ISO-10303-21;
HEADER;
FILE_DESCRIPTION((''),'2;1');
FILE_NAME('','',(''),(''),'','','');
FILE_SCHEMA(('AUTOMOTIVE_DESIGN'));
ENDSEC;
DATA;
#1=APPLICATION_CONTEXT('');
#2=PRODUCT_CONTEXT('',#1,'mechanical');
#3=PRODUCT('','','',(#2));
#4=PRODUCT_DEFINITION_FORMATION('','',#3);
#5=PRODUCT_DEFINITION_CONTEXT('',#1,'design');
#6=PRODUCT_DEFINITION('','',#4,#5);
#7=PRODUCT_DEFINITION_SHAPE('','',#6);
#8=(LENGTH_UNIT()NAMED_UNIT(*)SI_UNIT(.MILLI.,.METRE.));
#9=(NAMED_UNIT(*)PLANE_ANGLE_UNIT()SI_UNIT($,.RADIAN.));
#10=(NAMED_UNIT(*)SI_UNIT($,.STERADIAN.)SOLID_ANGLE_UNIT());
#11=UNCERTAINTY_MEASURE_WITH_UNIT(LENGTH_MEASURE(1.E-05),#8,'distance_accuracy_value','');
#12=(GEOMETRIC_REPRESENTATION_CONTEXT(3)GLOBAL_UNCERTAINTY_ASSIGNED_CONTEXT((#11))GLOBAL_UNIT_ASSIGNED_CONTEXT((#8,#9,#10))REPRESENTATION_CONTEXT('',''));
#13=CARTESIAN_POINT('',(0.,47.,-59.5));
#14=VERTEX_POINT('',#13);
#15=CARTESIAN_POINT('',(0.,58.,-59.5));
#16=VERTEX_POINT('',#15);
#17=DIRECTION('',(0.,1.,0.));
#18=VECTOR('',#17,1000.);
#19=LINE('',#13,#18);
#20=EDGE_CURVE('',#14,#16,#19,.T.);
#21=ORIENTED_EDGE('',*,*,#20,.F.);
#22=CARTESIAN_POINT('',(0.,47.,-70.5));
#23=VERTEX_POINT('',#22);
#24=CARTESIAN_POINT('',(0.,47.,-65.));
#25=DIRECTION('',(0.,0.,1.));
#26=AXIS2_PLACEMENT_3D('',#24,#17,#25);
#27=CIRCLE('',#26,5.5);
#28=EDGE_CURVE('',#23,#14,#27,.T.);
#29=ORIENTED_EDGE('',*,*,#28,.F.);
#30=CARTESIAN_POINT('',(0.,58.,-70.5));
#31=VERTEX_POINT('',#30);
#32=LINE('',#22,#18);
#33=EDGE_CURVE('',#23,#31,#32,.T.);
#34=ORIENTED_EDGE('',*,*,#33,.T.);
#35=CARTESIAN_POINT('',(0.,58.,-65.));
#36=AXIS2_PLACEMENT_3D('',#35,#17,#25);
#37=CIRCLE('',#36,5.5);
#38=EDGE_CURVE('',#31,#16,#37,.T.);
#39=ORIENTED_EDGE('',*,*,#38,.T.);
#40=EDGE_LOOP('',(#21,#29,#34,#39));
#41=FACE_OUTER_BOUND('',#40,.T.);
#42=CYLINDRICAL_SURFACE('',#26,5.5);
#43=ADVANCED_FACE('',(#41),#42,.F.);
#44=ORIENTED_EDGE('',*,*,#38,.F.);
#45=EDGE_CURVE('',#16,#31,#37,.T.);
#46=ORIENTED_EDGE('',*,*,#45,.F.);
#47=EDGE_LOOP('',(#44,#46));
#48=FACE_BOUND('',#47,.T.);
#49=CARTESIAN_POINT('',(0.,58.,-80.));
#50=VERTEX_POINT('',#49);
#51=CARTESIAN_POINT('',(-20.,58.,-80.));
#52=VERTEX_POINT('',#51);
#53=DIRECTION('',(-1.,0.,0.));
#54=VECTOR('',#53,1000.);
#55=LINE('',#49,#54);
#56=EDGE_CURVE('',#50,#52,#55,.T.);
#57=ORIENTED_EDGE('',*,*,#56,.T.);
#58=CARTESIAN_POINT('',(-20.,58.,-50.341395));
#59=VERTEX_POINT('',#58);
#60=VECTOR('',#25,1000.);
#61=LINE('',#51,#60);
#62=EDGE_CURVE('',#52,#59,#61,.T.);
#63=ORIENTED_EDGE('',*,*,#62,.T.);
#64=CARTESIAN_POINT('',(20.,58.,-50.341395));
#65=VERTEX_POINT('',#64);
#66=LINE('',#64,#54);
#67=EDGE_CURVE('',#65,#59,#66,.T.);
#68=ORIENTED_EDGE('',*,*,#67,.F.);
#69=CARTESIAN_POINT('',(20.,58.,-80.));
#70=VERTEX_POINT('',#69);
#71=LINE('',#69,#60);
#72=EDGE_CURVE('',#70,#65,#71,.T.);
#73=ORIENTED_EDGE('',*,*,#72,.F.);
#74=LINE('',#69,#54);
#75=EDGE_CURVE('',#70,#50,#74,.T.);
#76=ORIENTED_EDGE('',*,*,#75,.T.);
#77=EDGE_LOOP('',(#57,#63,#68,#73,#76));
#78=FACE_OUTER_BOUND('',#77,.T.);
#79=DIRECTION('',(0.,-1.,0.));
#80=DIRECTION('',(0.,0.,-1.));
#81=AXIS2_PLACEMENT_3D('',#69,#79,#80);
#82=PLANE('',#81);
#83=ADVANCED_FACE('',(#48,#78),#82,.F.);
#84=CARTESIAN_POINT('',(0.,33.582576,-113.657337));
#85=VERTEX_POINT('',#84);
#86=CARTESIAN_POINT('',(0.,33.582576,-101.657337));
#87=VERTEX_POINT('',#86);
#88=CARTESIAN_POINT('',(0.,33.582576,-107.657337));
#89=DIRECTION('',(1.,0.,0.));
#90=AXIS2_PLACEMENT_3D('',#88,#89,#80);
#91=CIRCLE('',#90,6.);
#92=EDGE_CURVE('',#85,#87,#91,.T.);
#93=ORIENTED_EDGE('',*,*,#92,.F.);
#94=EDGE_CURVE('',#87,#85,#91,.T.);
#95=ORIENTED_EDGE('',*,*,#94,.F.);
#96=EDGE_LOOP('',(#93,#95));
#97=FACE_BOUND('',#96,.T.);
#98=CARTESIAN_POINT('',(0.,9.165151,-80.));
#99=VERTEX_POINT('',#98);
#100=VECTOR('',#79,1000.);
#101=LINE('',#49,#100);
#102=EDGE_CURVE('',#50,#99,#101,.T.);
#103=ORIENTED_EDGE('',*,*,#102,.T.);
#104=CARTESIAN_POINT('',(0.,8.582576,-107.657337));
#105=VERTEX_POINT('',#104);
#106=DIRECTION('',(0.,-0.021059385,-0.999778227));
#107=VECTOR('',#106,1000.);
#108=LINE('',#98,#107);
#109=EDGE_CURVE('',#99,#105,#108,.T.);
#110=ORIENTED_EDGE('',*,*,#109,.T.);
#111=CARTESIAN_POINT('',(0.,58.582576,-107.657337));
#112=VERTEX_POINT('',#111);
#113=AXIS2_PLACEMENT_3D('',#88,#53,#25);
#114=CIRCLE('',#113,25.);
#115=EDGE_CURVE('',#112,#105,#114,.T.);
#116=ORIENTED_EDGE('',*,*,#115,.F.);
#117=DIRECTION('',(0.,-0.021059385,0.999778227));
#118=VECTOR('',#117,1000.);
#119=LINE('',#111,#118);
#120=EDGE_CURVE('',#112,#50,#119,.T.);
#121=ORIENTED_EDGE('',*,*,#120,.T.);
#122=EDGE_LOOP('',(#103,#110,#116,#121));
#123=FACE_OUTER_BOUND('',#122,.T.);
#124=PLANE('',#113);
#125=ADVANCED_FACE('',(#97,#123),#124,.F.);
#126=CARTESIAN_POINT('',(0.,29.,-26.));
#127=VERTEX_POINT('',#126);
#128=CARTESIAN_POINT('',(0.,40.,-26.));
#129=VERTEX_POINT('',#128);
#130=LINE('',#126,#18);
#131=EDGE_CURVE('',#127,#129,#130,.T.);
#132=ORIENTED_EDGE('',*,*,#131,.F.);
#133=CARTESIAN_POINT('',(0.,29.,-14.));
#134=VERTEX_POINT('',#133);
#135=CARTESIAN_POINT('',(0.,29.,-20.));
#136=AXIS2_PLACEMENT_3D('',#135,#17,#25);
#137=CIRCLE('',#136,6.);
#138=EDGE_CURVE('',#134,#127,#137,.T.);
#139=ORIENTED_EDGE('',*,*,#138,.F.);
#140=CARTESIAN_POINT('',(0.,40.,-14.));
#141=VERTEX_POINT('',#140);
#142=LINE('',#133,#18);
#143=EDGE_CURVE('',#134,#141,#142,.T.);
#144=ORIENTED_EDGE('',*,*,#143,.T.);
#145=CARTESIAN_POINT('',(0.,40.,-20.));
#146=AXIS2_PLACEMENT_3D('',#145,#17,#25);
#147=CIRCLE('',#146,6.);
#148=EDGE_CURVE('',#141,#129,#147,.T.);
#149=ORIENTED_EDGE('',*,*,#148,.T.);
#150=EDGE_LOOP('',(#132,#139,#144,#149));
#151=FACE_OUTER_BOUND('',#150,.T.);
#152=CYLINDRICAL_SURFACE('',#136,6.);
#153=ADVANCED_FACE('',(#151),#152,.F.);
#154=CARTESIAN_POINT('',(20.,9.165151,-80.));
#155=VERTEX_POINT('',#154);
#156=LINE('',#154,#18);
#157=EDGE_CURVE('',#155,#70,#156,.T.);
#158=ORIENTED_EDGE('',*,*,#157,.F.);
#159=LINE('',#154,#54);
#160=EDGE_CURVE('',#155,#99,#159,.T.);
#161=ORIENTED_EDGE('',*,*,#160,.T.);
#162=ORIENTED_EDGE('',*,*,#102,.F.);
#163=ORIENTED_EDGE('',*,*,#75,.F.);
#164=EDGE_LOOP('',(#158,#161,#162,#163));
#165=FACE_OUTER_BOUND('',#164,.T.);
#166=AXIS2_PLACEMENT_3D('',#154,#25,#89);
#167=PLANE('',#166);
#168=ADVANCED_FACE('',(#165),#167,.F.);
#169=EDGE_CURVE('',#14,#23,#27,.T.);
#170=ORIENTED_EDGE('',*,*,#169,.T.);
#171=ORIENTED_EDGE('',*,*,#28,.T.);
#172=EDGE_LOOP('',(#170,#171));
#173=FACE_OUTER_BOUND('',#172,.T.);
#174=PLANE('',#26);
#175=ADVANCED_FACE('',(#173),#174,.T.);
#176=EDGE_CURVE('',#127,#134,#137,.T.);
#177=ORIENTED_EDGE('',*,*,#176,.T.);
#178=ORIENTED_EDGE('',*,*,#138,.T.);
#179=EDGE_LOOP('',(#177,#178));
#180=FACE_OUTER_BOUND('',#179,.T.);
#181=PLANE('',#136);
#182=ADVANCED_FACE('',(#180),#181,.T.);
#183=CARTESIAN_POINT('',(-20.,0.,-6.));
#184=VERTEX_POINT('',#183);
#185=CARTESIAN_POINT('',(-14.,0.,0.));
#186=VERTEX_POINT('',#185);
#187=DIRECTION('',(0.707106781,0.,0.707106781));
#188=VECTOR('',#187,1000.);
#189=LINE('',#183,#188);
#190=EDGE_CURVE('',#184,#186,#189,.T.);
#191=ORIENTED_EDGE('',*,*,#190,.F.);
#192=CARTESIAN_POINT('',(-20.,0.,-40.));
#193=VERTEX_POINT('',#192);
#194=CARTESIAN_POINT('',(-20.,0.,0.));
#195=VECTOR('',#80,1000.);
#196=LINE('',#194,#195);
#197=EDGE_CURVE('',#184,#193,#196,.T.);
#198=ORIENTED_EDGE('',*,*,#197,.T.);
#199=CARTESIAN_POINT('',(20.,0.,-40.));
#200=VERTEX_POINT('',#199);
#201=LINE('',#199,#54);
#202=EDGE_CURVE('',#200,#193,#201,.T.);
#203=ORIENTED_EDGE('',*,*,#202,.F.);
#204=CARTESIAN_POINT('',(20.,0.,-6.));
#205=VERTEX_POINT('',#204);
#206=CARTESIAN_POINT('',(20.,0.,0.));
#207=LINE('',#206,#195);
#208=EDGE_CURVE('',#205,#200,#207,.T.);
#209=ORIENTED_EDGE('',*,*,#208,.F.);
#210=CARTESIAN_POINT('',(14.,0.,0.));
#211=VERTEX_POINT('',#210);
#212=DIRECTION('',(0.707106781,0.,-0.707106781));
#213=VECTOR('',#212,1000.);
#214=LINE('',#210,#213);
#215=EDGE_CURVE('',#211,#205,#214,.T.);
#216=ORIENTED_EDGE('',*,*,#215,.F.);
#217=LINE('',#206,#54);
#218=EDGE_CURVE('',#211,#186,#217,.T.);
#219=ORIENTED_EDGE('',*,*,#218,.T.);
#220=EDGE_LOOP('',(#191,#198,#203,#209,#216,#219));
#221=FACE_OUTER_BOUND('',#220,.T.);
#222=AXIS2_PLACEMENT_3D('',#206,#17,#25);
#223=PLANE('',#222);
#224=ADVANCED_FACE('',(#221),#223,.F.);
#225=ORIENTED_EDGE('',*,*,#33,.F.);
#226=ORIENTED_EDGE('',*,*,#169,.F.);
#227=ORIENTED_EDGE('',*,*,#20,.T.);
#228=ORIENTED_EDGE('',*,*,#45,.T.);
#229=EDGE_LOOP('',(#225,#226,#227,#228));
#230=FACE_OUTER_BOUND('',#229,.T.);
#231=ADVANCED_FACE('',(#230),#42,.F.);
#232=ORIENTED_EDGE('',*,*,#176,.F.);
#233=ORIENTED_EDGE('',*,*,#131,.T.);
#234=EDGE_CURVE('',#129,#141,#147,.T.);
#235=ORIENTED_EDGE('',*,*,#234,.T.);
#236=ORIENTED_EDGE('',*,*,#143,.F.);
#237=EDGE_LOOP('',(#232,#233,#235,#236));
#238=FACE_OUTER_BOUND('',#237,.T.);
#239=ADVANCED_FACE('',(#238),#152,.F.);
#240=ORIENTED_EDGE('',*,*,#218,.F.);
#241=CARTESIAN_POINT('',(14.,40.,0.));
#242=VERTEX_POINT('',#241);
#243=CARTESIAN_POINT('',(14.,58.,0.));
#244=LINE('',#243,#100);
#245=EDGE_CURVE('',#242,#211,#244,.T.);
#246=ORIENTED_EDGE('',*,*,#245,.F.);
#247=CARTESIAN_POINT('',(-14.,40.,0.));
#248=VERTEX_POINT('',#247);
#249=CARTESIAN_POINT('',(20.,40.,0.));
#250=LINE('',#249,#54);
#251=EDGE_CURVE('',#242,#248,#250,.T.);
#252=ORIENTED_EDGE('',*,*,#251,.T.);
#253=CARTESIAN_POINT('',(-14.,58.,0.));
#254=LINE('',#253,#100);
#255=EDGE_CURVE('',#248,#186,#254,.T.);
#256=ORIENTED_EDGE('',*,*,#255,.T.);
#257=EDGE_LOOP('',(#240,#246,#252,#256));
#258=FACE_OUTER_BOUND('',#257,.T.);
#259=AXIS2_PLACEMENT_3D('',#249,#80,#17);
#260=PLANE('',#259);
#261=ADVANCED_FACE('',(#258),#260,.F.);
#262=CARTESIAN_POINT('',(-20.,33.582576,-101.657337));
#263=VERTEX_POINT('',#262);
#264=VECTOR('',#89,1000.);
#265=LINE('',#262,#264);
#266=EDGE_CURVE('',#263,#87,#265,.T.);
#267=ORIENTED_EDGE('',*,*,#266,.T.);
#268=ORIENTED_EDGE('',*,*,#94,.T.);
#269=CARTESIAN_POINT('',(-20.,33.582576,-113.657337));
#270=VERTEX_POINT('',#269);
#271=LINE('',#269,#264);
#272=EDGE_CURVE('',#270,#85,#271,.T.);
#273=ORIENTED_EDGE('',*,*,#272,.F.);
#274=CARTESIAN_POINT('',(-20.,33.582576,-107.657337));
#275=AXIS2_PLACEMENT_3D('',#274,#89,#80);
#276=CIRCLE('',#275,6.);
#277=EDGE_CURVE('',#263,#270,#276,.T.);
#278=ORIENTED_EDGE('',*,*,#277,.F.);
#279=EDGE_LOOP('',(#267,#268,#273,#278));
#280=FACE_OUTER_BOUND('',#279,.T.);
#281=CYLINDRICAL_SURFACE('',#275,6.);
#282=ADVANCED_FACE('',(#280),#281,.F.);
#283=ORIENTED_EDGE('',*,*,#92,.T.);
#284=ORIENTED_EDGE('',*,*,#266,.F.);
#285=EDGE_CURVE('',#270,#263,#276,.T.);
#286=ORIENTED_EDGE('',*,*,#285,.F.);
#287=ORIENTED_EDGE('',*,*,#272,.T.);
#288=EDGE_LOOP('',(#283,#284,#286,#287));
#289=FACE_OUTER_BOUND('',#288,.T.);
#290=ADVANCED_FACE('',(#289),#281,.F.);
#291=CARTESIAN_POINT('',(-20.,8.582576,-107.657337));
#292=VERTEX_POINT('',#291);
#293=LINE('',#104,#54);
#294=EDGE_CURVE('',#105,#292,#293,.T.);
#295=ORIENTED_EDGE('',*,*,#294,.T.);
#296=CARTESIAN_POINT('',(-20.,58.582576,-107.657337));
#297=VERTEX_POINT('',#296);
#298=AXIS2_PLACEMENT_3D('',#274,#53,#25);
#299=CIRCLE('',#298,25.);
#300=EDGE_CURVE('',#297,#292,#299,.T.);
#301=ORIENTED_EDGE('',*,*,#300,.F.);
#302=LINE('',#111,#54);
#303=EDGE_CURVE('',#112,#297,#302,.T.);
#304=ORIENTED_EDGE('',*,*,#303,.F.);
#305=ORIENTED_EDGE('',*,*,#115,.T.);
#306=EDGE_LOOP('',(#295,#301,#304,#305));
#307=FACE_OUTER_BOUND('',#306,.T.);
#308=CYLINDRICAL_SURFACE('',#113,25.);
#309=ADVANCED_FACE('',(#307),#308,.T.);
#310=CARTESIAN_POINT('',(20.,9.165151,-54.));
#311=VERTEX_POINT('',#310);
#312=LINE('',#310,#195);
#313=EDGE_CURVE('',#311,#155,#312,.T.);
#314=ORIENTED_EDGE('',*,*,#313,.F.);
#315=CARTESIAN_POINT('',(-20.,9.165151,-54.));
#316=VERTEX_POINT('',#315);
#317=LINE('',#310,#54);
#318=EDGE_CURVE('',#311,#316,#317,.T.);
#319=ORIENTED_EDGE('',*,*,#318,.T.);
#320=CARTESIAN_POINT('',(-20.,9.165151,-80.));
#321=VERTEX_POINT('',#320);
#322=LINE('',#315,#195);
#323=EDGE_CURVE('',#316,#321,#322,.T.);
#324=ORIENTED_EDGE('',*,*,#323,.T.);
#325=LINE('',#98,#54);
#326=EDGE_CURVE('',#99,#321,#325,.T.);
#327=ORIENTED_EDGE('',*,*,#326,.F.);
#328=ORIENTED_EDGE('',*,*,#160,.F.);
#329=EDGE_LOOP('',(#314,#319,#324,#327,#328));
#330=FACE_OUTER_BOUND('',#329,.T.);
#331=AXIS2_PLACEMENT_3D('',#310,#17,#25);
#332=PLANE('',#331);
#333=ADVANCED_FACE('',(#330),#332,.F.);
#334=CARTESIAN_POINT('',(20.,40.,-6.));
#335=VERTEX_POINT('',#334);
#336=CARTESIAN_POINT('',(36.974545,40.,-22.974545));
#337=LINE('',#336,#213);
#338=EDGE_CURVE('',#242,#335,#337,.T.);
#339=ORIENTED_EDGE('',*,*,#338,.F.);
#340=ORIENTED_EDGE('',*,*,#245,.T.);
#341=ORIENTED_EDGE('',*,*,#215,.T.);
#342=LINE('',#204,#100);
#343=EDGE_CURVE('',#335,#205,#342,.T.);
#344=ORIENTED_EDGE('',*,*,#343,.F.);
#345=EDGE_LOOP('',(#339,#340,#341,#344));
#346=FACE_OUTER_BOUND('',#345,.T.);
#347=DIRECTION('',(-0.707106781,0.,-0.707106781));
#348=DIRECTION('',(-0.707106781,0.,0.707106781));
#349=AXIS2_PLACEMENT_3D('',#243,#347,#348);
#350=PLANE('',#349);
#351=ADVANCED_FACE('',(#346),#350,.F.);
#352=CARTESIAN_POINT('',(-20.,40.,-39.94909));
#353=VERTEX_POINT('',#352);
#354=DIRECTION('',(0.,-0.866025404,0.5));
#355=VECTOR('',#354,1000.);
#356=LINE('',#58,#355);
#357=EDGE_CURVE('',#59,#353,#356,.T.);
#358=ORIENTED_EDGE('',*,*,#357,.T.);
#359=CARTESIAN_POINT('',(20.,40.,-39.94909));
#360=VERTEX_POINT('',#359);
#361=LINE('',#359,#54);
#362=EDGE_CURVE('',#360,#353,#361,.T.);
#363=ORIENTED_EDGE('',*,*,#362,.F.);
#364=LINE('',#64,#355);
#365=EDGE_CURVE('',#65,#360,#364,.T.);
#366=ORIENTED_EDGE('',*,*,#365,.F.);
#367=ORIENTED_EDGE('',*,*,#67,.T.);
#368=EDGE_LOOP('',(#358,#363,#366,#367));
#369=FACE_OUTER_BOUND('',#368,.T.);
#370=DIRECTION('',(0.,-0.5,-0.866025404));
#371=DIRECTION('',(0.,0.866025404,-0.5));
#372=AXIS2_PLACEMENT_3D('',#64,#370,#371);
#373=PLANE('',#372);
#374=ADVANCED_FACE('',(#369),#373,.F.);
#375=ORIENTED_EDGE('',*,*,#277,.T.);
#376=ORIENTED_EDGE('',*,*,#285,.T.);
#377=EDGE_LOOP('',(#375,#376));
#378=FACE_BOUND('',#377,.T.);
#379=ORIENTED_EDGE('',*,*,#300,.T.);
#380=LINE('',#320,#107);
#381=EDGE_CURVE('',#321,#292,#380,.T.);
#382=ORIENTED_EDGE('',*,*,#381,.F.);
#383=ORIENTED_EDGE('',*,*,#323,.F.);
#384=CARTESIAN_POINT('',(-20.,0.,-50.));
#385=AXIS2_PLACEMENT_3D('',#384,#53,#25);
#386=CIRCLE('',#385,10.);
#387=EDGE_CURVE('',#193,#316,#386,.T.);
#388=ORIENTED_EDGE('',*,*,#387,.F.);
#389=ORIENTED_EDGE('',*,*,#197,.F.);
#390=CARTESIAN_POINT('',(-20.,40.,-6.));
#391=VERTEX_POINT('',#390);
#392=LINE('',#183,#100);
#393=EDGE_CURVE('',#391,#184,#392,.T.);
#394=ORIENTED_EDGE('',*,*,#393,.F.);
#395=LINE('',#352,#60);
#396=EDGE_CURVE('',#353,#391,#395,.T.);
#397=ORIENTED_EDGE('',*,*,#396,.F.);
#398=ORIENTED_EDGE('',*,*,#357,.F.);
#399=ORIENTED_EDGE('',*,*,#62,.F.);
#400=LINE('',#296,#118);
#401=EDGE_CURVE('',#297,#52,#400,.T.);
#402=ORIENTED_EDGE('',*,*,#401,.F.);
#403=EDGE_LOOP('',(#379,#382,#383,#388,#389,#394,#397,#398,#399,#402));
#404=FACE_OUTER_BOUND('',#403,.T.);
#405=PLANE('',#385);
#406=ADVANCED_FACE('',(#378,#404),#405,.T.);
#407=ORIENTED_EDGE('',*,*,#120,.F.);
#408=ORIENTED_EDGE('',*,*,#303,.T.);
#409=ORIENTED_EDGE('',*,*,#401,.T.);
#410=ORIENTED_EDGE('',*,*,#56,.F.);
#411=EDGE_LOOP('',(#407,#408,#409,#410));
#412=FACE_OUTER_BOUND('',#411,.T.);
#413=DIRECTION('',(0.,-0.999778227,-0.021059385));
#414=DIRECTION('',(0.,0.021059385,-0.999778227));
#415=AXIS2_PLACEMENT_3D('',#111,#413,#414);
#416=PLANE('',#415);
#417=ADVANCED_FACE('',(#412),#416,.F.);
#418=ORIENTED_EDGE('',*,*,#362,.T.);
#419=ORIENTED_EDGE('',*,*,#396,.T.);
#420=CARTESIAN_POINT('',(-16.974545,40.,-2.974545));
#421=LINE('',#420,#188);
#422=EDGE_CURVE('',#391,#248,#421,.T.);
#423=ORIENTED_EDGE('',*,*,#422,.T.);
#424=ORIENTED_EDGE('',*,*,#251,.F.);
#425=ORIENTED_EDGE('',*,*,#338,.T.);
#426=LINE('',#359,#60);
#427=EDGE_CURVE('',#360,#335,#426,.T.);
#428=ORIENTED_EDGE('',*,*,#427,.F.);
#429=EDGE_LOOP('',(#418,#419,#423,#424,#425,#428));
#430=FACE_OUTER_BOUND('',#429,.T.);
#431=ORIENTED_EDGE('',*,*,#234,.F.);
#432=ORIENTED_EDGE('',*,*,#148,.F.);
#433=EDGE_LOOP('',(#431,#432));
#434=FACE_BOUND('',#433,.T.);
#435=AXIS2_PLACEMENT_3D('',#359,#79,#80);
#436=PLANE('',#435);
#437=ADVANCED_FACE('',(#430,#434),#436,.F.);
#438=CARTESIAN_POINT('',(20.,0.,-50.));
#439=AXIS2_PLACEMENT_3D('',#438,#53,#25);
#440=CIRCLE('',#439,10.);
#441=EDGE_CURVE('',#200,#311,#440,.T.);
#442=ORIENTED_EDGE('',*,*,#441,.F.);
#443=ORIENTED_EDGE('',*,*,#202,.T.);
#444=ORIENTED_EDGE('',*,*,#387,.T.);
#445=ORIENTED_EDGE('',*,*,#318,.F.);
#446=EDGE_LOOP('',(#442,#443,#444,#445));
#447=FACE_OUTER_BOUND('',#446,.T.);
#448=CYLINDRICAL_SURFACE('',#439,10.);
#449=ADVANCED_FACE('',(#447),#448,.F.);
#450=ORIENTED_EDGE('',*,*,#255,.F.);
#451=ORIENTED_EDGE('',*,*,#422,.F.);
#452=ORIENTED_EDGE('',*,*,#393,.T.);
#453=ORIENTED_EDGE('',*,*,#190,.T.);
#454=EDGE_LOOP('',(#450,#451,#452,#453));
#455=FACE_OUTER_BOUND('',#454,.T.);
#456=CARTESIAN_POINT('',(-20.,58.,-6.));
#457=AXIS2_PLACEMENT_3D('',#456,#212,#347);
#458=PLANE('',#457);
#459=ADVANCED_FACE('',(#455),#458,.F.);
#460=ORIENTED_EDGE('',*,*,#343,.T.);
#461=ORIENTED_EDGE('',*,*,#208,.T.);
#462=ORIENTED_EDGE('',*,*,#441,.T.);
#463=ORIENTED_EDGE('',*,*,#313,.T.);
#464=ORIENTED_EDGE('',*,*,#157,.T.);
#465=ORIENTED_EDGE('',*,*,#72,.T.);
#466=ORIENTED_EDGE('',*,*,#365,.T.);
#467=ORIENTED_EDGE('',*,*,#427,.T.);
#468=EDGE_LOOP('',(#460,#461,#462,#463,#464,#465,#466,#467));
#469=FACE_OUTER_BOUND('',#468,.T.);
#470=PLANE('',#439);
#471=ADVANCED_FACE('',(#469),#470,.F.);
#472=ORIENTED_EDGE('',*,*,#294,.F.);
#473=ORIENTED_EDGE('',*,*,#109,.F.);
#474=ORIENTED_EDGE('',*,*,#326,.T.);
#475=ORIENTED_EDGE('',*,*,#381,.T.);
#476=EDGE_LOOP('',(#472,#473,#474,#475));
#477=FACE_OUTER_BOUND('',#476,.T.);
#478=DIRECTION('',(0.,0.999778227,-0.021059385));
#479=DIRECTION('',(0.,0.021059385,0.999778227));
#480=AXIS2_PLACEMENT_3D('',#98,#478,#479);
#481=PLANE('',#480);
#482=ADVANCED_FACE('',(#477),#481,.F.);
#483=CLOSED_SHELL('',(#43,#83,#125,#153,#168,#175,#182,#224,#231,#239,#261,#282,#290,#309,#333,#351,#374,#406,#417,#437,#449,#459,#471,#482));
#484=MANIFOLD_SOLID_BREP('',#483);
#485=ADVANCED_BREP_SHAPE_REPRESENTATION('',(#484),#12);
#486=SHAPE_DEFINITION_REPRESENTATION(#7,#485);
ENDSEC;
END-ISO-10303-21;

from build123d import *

# Parameters (mm, degrees)
HOUSING_BODY_DEPTH       = 20
CORNER_CUT_A_6X6_DEPTH   = 101.816665289
CORNER_CUT_B_6X6_DEPTH   = 101.816665289
STEP_HOLE_SKETCH_R       = 6
STEP_HOLE_CUT_DEPTH      = 11
SECOND_STEP_CUT_SKETCH_R = 5.5
SECOND_STEP_CUT_DEPTH    = 11
EYE_LUG_DEPTH            = 20
EYE_BORE_SKETCH_R        = 6
EYE_BORE_12_DEPTH        = 147.389505053


with BuildPart() as part:
    # Housing Profile Sketch → Housing Body (new, symmetric)
    with BuildSketch(Plane(origin=(0, 0, 0), x_dir=(0, 0, -1), z_dir=(1, 0, 0))):
        with BuildLine():
            Line((0, 0), (40, 0))
            ThreePointArc((40, 0), (44.522774425, 8.366600265), (54, 9.16515139))
            Line((54, 9.16515139), (80, 9.16515139))
            Line((80, 9.16515139), (80, 58))
            Line((80, 58), (50.341394733, 58))
            Line((50.341394733, 58), (39.949089887, 40))
            Line((39.949089887, 40), (0, 40))
            Line((0, 40), (0, 0))
        make_face()
    extrude(amount=HOUSING_BODY_DEPTH, both=True)

    # Corner Cut A Sketch → Corner Cut A 6x6 (cut, through all)
    with BuildSketch(Plane.XZ):
        Polygon((14, 0), (20, -6), (20, 0), align=None)
    extrude(amount=-CORNER_CUT_A_6X6_DEPTH, mode=Mode.SUBTRACT)

    # Corner Cut B Sketch → Corner Cut B 6x6 (cut, through all)
    with BuildSketch(Plane.XZ):
        Polygon((-20, 0), (-20, -6), (-14, 0), align=None)
    extrude(amount=-CORNER_CUT_B_6X6_DEPTH, mode=Mode.SUBTRACT)

    # Step Hole Sketch → Step Hole Cut (cut)
    with BuildSketch(Plane(origin=(0, 40, 0), x_dir=(1, 0, 0), z_dir=(0, 1, 0))):
        with Locations(Location((0, 20, 0), (0, 0, 270))):
            Circle(STEP_HOLE_SKETCH_R)
    extrude(amount=-STEP_HOLE_CUT_DEPTH, mode=Mode.SUBTRACT)

    # Second Step Cut Sketch → Second Step Cut (cut)
    with BuildSketch(Plane(origin=(0, 58, 0), x_dir=(1, 0, 0), z_dir=(0, 1, 0))):
        with Locations(Location((0, 65, 0), (0, 0, 270))):
            Circle(SECOND_STEP_CUT_SKETCH_R)
    extrude(amount=-SECOND_STEP_CUT_DEPTH, mode=Mode.SUBTRACT)

    # Eye Lug Sketch → Eye Lug (add)
    with BuildSketch(Plane.ZY.offset(20)):
        with BuildLine():
            Line((-107.657336829, 58.582575695), (-80, 58))
            Line((-80, 58), (-80, 9.16515139))
            Line((-80, 9.16515139), (-107.657336829, 8.582575695))
            ThreePointArc((-107.657336829, 8.582575695), (-132.657336829, 33.582575695), (-107.657336829, 58.582575695))
        make_face()
    extrude(amount=-EYE_LUG_DEPTH)

    # Eye Bore Sketch → Eye Bore Ø12 (cut, through all)
    with BuildSketch(Plane(origin=(0, 0, 0), x_dir=(0, 0, -1), z_dir=(1, 0, 0))):
        with Locations((107.657336829, 33.582575695)):
            Circle(EYE_BORE_SKETCH_R)
    extrude(amount=-EYE_BORE_12_DEPTH, mode=Mode.SUBTRACT)


solid = part.part
